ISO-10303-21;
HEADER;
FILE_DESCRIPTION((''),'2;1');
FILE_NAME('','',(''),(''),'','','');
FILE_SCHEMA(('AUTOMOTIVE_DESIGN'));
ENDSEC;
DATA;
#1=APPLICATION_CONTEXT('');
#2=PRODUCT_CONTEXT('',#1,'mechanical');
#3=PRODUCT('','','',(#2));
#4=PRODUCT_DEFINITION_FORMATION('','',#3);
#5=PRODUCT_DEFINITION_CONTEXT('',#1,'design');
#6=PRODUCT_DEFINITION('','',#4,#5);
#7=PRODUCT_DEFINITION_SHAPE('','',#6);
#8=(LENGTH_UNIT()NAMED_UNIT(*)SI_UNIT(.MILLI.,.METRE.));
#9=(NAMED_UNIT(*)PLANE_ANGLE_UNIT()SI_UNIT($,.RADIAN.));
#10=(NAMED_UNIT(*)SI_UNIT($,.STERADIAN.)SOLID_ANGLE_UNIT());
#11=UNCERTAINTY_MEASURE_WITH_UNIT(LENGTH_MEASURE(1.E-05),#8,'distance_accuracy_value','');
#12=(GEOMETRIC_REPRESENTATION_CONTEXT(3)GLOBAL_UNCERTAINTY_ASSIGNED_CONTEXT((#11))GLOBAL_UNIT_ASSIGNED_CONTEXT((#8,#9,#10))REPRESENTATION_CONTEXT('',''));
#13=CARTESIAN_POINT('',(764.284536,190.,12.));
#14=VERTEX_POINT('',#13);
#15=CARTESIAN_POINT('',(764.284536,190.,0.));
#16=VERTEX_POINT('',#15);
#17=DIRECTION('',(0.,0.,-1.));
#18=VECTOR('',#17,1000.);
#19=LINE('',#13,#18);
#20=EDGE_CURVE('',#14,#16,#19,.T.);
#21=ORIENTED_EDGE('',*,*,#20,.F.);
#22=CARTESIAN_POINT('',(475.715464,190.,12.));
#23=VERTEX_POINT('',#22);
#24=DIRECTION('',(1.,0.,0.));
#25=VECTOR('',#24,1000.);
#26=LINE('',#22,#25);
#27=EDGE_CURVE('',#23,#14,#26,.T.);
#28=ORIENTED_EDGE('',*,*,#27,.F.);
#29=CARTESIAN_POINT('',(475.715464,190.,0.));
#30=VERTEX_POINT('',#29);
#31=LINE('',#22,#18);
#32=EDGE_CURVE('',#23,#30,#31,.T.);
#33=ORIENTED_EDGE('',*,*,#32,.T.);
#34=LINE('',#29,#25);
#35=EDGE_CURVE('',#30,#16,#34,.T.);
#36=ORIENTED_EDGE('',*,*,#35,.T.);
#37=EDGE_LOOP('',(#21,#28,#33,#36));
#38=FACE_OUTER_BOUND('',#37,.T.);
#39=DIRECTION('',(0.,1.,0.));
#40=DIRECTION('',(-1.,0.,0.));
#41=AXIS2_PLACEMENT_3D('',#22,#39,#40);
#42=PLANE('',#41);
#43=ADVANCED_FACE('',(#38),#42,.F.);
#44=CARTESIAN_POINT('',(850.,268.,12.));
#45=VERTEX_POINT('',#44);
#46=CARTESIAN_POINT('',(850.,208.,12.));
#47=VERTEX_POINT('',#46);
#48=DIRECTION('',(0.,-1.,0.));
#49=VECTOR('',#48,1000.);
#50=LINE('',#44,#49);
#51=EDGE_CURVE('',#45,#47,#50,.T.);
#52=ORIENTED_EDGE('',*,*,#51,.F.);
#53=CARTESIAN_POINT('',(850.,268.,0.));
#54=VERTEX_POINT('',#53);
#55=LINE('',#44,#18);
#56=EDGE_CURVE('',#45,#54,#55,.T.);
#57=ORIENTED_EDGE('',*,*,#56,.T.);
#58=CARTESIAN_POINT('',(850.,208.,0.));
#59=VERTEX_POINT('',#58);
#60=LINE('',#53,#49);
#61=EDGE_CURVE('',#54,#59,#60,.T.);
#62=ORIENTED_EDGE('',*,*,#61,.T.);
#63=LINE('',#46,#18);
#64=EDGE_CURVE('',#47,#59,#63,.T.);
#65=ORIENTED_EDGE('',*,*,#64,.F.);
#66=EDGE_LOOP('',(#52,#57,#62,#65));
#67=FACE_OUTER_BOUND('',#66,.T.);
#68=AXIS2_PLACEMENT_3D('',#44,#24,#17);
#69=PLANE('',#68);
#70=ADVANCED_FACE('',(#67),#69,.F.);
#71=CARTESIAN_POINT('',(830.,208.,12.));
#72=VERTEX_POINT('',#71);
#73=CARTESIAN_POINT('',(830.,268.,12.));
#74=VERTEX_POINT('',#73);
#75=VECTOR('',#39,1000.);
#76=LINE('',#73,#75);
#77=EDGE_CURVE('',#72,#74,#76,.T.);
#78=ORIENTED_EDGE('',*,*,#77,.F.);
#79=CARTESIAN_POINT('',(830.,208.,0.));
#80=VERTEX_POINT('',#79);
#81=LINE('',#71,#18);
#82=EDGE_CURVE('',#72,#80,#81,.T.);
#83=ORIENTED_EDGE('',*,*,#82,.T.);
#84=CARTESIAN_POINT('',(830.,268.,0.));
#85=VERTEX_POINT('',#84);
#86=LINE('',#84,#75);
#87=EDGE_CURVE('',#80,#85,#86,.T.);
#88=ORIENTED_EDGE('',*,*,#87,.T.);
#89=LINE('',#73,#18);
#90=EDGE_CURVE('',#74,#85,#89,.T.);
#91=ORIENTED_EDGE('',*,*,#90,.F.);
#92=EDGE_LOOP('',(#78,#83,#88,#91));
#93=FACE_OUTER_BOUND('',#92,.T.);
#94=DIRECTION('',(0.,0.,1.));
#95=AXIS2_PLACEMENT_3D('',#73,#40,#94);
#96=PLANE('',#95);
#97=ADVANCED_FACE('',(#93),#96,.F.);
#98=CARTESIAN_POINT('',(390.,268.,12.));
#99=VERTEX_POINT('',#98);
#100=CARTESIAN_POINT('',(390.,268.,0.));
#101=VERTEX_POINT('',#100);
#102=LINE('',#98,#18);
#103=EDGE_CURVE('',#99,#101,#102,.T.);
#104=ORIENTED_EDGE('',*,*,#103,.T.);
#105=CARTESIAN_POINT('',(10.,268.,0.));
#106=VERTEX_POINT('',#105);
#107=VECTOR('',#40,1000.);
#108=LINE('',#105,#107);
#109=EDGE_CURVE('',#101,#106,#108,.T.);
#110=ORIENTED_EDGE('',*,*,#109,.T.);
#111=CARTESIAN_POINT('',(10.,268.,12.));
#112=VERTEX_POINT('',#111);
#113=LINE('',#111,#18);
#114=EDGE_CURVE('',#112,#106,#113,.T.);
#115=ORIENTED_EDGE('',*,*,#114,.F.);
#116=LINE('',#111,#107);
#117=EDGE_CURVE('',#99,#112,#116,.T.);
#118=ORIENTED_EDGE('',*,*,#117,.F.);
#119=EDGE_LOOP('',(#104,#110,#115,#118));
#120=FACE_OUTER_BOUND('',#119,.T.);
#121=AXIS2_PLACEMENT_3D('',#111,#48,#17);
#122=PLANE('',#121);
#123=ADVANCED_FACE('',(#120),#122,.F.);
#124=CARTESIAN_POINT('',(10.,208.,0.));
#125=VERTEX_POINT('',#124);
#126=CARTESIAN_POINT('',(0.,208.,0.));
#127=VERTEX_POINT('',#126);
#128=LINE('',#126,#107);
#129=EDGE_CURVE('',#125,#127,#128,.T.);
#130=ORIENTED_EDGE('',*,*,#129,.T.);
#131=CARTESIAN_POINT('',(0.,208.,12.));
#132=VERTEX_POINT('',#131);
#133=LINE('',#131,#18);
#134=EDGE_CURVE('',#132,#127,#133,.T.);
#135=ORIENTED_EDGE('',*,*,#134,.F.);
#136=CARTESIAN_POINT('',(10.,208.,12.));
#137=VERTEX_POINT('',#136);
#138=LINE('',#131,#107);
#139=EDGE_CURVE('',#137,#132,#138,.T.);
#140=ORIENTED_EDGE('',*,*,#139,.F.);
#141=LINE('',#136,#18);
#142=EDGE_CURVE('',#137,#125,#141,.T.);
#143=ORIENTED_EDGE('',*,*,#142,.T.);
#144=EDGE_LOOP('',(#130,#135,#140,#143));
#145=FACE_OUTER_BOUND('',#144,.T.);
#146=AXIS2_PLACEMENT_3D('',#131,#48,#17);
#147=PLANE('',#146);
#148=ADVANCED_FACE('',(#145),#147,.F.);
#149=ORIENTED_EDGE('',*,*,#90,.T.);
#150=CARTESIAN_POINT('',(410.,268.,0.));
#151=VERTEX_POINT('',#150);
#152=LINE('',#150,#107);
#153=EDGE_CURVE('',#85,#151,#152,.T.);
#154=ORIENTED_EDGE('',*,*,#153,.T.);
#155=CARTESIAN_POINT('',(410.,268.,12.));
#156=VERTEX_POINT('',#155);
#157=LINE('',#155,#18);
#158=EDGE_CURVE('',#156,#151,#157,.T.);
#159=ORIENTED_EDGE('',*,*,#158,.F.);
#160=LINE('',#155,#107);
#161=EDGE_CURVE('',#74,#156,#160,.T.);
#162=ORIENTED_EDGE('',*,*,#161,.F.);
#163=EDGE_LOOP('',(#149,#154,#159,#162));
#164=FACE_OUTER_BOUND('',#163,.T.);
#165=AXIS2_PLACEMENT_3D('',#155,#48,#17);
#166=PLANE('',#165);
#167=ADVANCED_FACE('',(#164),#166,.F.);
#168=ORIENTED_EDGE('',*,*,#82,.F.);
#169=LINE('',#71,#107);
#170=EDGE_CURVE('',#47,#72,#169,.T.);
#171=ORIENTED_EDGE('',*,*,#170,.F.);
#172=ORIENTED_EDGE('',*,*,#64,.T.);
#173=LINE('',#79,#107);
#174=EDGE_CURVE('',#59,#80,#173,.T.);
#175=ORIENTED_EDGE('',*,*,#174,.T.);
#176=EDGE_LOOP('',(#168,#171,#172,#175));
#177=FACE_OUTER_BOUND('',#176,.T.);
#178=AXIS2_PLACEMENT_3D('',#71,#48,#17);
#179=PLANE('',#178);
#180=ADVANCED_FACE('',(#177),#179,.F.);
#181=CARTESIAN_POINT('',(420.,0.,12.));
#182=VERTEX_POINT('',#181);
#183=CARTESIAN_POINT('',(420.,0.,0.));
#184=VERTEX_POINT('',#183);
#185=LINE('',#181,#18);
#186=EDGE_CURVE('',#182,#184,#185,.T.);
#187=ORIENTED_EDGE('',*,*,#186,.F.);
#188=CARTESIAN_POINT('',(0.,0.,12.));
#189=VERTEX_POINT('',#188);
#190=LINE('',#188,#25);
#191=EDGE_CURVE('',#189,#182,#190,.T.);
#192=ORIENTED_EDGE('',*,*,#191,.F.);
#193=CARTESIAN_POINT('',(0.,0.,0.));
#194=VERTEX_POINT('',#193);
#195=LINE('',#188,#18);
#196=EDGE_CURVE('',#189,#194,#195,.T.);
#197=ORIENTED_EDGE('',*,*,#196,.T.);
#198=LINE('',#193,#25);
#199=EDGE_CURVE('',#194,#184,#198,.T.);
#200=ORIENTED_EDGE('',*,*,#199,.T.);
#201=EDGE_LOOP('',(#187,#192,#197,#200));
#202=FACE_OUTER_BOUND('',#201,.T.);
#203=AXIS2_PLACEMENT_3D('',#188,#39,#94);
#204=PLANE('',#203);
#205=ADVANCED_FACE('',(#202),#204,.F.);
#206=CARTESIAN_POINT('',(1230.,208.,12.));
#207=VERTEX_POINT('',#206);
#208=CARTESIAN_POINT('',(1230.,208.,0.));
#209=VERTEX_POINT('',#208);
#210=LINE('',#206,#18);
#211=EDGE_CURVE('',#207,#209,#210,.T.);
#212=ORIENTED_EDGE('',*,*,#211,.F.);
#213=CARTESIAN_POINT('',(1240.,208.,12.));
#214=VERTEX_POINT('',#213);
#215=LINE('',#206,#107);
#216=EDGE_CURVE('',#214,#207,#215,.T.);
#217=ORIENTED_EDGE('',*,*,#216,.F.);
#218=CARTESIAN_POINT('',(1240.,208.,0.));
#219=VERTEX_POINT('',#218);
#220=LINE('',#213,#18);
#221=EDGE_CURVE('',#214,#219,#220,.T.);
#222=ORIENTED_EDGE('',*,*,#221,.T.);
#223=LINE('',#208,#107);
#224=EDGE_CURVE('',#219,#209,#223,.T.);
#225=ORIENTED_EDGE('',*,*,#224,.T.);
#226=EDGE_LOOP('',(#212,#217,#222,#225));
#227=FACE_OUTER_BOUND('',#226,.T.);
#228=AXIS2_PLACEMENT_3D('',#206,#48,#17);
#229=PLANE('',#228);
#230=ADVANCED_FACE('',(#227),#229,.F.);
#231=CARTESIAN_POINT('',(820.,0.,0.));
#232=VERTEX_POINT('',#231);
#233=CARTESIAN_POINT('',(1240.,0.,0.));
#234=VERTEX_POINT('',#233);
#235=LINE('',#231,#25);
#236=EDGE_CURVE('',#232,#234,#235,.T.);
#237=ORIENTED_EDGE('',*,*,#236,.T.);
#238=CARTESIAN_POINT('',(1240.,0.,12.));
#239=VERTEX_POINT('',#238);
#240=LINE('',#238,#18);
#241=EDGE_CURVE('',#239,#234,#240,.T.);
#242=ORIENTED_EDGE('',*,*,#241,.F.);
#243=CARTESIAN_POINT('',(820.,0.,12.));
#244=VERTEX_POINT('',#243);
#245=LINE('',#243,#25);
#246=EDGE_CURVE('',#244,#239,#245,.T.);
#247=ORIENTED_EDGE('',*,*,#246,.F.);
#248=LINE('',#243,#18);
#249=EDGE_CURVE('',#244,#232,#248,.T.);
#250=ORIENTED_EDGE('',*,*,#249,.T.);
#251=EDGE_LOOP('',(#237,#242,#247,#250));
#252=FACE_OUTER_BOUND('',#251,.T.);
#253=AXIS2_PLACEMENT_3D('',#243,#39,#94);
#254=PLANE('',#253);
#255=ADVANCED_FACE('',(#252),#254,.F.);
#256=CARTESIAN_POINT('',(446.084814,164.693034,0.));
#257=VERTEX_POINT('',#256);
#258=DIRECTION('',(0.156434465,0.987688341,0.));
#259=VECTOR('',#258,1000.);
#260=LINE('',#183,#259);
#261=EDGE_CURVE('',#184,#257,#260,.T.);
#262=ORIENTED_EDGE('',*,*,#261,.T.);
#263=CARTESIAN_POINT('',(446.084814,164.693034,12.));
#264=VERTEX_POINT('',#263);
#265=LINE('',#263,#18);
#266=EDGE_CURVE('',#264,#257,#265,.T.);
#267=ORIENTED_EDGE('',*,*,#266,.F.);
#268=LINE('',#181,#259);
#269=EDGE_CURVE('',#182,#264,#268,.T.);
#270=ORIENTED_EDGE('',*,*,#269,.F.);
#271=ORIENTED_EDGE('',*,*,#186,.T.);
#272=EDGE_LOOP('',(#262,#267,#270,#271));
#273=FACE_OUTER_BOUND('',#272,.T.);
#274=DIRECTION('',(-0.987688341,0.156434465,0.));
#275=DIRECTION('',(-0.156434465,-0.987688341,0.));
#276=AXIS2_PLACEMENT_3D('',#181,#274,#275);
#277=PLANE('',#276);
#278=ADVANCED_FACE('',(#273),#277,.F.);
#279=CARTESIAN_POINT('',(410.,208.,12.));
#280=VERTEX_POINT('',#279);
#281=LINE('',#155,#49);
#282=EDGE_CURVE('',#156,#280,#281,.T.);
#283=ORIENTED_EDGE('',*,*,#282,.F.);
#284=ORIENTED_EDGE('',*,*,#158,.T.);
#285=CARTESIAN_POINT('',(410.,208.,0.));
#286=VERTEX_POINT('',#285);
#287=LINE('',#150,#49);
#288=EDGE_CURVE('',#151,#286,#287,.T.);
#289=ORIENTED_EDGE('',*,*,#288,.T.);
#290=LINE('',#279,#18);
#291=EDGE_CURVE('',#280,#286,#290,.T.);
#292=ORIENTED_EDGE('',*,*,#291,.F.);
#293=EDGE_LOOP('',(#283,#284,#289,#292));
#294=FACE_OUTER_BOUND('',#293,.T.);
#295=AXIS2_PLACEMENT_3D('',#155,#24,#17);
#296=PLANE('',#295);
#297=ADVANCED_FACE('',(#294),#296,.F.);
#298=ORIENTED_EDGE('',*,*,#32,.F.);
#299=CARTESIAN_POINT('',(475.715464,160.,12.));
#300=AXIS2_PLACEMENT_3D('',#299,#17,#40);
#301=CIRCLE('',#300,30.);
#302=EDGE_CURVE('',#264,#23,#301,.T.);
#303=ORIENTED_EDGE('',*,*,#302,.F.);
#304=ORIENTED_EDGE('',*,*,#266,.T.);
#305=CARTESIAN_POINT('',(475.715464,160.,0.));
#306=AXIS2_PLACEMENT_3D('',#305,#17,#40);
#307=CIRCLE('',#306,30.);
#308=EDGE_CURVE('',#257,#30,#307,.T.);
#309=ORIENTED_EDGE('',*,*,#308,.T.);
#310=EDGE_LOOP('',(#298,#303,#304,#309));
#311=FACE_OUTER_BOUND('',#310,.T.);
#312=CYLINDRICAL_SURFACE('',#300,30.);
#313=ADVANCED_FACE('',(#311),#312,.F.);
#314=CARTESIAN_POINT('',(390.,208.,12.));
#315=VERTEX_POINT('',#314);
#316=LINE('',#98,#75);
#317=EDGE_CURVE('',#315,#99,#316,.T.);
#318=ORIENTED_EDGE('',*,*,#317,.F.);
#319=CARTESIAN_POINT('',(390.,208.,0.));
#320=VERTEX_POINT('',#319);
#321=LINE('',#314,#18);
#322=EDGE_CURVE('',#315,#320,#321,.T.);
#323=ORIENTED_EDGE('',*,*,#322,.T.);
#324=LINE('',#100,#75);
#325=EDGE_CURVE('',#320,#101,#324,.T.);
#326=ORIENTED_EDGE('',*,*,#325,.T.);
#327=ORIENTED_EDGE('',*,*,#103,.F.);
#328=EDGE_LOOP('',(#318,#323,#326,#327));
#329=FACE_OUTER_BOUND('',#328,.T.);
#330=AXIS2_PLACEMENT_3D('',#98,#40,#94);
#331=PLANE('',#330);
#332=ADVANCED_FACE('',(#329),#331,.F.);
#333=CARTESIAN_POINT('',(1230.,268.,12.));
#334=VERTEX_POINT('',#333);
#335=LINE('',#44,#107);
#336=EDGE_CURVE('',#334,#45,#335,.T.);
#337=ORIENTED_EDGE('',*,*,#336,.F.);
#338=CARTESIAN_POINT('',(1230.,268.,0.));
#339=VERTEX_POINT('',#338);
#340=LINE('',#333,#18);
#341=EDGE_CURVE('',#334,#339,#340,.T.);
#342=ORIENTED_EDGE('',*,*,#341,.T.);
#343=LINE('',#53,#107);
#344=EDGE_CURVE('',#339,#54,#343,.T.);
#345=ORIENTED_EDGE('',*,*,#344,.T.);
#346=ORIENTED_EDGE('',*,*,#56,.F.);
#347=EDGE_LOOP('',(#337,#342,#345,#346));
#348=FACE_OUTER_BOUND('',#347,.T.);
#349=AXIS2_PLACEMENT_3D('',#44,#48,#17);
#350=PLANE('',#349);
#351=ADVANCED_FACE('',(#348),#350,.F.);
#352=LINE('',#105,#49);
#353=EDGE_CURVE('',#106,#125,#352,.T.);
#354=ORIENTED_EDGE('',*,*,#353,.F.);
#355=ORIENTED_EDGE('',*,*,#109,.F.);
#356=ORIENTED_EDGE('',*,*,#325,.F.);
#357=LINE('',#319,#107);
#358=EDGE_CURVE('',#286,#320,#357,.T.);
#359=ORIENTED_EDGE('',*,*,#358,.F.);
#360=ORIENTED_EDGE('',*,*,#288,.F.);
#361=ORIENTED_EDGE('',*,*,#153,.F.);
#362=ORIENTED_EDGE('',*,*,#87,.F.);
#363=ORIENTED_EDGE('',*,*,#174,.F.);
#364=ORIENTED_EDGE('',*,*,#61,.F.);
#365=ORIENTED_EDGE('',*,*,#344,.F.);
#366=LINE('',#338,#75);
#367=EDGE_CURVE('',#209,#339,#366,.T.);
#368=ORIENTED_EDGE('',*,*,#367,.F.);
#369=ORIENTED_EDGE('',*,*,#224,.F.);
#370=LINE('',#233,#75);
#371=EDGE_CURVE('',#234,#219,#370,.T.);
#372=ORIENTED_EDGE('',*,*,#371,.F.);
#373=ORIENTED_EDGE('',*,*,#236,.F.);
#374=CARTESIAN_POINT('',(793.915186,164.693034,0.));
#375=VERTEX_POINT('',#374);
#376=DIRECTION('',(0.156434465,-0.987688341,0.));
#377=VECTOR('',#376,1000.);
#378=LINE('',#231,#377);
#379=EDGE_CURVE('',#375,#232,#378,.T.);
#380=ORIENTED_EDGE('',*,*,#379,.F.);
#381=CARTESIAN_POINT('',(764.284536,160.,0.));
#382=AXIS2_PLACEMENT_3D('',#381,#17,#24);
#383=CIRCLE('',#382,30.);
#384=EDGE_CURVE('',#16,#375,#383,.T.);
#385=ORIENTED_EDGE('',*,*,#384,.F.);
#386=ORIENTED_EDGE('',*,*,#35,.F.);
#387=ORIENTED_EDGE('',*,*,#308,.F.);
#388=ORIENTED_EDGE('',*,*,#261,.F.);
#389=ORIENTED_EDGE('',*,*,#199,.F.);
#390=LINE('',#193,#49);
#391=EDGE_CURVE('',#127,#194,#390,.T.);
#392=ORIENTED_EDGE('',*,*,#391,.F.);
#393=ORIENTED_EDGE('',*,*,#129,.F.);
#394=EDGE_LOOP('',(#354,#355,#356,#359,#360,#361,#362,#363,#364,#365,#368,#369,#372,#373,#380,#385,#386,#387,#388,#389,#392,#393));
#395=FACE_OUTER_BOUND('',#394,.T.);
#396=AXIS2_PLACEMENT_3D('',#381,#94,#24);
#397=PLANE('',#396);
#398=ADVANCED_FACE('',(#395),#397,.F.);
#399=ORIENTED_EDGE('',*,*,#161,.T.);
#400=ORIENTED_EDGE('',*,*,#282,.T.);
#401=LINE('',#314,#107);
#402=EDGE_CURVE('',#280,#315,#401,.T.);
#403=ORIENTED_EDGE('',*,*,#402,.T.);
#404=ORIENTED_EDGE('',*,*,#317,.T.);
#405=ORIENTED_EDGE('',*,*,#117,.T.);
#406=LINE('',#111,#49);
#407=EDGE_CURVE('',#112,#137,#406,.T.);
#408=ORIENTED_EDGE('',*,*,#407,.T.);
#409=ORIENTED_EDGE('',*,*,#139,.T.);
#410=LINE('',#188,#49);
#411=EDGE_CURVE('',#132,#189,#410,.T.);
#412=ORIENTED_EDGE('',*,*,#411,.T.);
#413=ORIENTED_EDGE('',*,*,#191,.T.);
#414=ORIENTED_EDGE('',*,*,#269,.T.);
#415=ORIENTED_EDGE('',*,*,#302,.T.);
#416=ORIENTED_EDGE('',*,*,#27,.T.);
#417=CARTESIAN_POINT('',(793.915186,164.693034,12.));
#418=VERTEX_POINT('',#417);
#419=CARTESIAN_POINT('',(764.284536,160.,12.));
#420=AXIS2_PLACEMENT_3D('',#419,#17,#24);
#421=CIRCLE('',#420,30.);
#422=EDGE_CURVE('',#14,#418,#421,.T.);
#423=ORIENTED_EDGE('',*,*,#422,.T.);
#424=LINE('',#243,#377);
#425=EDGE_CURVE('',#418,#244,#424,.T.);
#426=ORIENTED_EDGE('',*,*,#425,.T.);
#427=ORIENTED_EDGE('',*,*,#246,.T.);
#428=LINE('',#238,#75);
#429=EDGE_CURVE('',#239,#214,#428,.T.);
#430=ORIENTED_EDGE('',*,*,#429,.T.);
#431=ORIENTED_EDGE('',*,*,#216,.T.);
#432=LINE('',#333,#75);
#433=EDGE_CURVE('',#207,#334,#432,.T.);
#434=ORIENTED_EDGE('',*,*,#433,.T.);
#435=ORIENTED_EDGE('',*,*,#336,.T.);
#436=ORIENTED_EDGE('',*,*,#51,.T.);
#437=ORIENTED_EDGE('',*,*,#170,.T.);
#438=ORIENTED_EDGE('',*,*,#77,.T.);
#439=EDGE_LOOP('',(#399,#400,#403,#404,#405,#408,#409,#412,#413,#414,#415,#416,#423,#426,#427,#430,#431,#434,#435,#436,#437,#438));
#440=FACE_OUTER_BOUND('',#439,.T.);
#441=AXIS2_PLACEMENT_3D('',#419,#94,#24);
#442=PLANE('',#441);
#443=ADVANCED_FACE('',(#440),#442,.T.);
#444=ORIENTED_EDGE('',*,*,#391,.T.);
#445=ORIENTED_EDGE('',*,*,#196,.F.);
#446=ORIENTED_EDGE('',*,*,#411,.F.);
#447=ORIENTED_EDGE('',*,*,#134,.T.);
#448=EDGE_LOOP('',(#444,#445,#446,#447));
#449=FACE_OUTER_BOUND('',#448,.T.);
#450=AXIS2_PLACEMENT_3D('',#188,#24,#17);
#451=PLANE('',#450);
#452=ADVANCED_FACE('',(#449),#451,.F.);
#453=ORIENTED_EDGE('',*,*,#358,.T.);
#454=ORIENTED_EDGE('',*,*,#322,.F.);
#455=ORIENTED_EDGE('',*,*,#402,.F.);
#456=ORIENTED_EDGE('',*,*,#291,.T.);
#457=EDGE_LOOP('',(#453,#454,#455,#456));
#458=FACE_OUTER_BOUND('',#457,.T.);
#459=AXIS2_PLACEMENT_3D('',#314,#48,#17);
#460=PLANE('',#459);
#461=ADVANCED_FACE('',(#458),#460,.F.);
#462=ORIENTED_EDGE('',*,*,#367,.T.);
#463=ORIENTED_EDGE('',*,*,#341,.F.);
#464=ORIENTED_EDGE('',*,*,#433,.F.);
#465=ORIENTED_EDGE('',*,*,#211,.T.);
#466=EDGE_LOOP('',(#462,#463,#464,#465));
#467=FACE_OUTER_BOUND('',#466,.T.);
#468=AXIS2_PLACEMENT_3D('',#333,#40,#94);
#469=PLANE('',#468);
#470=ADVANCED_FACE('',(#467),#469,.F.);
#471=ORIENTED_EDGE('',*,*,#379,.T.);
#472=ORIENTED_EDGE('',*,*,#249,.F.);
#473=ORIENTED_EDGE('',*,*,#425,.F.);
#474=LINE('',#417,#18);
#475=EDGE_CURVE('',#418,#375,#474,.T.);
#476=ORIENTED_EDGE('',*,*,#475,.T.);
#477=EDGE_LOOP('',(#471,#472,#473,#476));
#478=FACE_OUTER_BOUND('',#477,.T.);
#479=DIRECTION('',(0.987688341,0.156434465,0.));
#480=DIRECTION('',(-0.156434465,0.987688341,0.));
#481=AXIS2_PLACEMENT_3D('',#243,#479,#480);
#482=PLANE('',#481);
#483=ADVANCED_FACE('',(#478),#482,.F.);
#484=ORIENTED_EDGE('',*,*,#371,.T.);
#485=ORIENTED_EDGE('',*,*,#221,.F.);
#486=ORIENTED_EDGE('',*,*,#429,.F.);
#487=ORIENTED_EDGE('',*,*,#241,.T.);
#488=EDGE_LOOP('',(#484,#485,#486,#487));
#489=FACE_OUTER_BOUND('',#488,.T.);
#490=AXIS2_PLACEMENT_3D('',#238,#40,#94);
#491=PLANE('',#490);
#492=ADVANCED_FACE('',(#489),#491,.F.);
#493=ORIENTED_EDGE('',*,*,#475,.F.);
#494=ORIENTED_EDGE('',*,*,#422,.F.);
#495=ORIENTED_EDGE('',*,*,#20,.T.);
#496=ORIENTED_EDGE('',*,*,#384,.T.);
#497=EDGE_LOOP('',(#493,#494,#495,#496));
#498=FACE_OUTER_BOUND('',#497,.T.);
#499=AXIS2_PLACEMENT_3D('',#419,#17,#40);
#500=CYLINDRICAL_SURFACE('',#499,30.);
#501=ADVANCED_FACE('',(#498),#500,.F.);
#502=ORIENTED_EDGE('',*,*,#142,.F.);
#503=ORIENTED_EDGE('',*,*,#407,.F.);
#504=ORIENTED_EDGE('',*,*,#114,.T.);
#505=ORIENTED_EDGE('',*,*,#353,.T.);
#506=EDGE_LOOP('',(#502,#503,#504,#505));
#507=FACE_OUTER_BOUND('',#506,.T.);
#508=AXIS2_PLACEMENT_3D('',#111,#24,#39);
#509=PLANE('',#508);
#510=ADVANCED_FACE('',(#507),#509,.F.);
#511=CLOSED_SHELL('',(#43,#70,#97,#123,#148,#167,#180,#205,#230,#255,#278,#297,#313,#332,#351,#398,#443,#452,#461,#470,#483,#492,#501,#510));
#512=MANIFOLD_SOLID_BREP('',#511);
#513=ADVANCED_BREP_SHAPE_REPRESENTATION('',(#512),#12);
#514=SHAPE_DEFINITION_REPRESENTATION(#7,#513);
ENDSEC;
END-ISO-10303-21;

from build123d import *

# Parameters (mm, degrees)
BOSS_EXTRUDE1_DEPTH = 12


with BuildPart() as part:
    # Sketch1 → Boss-Extrude1 (new body)
    with BuildSketch(Plane.XY):
        with BuildLine():
            Line((0, 0), (420, 0))
            Line((420, 0), (446.084814008, 164.693033951))
            ThreePointArc((446.084814008, 164.693033951), (456.232022776, 182.812178968), (475.715464226, 190))
            Line((475.715464226, 190), (764.284535774, 190))
            ThreePointArc((764.284535774, 190), (783.767977224, 182.812178968), (793.915185992, 164.693033951))
            Line((793.915185992, 164.693033951), (820, 0))
            Line((820, 0), (1240, 0))
            Line((1240, 0), (1240, 208))
            Line((1240, 208), (1230, 208))
            Line((1230, 208), (1230, 268))
            Line((1230, 268), (850, 268))
            Line((850, 268), (850, 208))
            Line((850, 208), (830, 208))
            Line((830, 208), (830, 268))
            Line((830, 268), (410, 268))
            Line((410, 268), (410, 208))
            Line((410, 208), (390, 208))
            Line((390, 208), (390, 268))
            Line((390, 268), (10, 268))
            Line((10, 268), (10, 208))
            Line((10, 208), (0, 208))
            Line((0, 208), (0, 0))
        make_face()
    extrude(amount=BOSS_EXTRUDE1_DEPTH)


solid = part.part
